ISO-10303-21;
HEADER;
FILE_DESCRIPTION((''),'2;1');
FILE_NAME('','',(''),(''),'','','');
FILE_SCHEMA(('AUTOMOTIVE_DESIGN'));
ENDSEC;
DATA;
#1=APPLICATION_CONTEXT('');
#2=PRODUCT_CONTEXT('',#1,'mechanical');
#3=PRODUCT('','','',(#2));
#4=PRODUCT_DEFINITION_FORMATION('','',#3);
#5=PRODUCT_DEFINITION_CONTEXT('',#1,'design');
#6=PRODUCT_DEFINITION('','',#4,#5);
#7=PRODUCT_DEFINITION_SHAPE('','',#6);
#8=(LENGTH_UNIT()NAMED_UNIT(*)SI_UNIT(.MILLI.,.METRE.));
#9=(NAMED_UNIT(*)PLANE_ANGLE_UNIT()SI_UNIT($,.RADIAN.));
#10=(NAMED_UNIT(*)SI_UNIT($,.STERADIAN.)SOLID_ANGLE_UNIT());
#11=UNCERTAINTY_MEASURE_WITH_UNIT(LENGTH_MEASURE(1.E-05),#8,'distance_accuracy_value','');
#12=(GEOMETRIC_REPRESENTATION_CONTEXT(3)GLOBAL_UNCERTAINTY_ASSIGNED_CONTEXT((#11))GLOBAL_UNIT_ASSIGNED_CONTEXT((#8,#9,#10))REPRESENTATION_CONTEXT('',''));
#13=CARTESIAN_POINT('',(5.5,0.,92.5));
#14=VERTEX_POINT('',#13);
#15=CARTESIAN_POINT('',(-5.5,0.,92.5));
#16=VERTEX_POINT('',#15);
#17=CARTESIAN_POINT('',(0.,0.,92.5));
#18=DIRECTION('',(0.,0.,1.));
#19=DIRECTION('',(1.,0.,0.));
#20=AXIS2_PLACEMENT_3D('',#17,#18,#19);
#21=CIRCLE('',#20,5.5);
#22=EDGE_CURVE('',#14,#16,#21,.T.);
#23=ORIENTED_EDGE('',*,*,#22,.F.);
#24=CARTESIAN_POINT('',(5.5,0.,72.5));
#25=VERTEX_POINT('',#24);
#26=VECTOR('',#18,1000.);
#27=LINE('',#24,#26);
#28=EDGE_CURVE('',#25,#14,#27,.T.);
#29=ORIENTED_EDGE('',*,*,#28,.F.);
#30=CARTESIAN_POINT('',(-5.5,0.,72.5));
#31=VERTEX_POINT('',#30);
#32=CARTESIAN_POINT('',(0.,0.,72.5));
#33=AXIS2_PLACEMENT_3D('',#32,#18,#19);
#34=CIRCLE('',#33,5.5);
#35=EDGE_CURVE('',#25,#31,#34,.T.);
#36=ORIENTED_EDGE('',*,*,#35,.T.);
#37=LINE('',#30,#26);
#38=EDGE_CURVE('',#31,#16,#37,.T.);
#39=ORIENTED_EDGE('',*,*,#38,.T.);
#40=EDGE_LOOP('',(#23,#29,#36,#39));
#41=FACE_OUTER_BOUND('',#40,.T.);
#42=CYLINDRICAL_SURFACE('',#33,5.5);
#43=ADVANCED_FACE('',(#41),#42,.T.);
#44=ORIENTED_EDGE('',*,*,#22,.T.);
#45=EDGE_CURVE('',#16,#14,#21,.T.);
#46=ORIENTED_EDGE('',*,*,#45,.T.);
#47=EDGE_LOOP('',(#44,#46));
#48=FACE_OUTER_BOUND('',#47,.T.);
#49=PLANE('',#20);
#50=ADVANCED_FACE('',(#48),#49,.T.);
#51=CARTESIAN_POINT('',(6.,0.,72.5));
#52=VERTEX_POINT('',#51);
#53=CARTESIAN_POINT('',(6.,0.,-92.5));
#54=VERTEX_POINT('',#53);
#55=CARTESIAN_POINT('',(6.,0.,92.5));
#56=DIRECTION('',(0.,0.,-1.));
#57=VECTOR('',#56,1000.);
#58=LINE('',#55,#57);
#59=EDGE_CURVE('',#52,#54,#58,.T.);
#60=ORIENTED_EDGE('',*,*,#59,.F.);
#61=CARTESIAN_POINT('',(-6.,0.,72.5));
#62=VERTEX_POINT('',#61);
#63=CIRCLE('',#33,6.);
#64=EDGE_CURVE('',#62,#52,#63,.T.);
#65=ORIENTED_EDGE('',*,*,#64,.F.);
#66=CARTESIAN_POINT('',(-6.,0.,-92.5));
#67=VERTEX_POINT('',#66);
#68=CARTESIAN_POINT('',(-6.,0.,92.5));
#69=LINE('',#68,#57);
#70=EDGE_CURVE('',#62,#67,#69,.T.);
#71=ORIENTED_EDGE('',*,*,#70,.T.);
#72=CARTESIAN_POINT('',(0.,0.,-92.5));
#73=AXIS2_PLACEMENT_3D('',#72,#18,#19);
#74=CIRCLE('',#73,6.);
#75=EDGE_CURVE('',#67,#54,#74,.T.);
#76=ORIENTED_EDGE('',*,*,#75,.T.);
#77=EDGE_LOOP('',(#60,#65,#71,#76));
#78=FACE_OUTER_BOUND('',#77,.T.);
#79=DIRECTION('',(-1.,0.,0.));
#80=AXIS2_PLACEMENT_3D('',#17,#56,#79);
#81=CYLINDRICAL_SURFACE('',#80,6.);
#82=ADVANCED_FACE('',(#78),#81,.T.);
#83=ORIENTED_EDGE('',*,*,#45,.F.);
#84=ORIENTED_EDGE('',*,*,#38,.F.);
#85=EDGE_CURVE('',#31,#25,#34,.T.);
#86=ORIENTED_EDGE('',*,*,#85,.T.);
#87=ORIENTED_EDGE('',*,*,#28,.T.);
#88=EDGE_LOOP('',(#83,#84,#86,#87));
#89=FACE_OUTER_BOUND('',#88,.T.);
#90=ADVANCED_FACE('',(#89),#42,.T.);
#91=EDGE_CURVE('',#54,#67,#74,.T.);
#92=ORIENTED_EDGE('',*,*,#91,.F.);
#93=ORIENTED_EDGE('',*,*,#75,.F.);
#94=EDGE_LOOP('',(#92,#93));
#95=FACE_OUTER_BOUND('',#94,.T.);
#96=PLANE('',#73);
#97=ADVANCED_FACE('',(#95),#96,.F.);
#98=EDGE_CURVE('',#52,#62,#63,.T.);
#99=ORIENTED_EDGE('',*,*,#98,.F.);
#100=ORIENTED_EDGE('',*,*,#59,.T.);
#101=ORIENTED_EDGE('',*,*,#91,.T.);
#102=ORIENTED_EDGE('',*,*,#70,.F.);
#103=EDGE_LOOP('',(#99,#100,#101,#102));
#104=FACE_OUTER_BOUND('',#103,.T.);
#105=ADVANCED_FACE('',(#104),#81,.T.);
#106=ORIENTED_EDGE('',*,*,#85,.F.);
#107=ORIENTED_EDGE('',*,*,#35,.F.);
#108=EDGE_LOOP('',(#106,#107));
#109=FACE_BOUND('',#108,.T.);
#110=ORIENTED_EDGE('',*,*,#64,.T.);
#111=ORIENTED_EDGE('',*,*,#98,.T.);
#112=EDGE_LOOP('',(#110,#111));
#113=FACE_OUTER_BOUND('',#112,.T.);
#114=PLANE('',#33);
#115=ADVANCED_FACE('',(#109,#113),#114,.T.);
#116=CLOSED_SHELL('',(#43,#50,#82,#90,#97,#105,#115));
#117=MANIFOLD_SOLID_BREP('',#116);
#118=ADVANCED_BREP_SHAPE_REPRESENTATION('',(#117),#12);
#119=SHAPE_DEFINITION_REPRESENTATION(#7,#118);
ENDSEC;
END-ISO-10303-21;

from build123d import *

# Parameters (mm, degrees)
SKETCH_1_R          = 6
EXTRUDE_3_DEPTH     = 92.5
SKETCH_3_R          = 6
SKETCH_3_R_2        = 5.5
CUT_EXTRUDE_1_DEPTH = 20


with BuildPart() as part:
    # 草图1 → 凸台-拉伸3 (new, symmetric)
    with BuildSketch(Plane.XY):
        Circle(SKETCH_1_R)
    extrude(amount=EXTRUDE_3_DEPTH, both=True)

    # 草图3 → 切除-拉伸1 (cut)
    with BuildSketch(Plane.XY.offset(92.5)):
        Circle(SKETCH_3_R)
        Circle(SKETCH_3_R_2, mode=Mode.SUBTRACT)
    extrude(amount=-CUT_EXTRUDE_1_DEPTH, mode=Mode.SUBTRACT)


solid = part.part
